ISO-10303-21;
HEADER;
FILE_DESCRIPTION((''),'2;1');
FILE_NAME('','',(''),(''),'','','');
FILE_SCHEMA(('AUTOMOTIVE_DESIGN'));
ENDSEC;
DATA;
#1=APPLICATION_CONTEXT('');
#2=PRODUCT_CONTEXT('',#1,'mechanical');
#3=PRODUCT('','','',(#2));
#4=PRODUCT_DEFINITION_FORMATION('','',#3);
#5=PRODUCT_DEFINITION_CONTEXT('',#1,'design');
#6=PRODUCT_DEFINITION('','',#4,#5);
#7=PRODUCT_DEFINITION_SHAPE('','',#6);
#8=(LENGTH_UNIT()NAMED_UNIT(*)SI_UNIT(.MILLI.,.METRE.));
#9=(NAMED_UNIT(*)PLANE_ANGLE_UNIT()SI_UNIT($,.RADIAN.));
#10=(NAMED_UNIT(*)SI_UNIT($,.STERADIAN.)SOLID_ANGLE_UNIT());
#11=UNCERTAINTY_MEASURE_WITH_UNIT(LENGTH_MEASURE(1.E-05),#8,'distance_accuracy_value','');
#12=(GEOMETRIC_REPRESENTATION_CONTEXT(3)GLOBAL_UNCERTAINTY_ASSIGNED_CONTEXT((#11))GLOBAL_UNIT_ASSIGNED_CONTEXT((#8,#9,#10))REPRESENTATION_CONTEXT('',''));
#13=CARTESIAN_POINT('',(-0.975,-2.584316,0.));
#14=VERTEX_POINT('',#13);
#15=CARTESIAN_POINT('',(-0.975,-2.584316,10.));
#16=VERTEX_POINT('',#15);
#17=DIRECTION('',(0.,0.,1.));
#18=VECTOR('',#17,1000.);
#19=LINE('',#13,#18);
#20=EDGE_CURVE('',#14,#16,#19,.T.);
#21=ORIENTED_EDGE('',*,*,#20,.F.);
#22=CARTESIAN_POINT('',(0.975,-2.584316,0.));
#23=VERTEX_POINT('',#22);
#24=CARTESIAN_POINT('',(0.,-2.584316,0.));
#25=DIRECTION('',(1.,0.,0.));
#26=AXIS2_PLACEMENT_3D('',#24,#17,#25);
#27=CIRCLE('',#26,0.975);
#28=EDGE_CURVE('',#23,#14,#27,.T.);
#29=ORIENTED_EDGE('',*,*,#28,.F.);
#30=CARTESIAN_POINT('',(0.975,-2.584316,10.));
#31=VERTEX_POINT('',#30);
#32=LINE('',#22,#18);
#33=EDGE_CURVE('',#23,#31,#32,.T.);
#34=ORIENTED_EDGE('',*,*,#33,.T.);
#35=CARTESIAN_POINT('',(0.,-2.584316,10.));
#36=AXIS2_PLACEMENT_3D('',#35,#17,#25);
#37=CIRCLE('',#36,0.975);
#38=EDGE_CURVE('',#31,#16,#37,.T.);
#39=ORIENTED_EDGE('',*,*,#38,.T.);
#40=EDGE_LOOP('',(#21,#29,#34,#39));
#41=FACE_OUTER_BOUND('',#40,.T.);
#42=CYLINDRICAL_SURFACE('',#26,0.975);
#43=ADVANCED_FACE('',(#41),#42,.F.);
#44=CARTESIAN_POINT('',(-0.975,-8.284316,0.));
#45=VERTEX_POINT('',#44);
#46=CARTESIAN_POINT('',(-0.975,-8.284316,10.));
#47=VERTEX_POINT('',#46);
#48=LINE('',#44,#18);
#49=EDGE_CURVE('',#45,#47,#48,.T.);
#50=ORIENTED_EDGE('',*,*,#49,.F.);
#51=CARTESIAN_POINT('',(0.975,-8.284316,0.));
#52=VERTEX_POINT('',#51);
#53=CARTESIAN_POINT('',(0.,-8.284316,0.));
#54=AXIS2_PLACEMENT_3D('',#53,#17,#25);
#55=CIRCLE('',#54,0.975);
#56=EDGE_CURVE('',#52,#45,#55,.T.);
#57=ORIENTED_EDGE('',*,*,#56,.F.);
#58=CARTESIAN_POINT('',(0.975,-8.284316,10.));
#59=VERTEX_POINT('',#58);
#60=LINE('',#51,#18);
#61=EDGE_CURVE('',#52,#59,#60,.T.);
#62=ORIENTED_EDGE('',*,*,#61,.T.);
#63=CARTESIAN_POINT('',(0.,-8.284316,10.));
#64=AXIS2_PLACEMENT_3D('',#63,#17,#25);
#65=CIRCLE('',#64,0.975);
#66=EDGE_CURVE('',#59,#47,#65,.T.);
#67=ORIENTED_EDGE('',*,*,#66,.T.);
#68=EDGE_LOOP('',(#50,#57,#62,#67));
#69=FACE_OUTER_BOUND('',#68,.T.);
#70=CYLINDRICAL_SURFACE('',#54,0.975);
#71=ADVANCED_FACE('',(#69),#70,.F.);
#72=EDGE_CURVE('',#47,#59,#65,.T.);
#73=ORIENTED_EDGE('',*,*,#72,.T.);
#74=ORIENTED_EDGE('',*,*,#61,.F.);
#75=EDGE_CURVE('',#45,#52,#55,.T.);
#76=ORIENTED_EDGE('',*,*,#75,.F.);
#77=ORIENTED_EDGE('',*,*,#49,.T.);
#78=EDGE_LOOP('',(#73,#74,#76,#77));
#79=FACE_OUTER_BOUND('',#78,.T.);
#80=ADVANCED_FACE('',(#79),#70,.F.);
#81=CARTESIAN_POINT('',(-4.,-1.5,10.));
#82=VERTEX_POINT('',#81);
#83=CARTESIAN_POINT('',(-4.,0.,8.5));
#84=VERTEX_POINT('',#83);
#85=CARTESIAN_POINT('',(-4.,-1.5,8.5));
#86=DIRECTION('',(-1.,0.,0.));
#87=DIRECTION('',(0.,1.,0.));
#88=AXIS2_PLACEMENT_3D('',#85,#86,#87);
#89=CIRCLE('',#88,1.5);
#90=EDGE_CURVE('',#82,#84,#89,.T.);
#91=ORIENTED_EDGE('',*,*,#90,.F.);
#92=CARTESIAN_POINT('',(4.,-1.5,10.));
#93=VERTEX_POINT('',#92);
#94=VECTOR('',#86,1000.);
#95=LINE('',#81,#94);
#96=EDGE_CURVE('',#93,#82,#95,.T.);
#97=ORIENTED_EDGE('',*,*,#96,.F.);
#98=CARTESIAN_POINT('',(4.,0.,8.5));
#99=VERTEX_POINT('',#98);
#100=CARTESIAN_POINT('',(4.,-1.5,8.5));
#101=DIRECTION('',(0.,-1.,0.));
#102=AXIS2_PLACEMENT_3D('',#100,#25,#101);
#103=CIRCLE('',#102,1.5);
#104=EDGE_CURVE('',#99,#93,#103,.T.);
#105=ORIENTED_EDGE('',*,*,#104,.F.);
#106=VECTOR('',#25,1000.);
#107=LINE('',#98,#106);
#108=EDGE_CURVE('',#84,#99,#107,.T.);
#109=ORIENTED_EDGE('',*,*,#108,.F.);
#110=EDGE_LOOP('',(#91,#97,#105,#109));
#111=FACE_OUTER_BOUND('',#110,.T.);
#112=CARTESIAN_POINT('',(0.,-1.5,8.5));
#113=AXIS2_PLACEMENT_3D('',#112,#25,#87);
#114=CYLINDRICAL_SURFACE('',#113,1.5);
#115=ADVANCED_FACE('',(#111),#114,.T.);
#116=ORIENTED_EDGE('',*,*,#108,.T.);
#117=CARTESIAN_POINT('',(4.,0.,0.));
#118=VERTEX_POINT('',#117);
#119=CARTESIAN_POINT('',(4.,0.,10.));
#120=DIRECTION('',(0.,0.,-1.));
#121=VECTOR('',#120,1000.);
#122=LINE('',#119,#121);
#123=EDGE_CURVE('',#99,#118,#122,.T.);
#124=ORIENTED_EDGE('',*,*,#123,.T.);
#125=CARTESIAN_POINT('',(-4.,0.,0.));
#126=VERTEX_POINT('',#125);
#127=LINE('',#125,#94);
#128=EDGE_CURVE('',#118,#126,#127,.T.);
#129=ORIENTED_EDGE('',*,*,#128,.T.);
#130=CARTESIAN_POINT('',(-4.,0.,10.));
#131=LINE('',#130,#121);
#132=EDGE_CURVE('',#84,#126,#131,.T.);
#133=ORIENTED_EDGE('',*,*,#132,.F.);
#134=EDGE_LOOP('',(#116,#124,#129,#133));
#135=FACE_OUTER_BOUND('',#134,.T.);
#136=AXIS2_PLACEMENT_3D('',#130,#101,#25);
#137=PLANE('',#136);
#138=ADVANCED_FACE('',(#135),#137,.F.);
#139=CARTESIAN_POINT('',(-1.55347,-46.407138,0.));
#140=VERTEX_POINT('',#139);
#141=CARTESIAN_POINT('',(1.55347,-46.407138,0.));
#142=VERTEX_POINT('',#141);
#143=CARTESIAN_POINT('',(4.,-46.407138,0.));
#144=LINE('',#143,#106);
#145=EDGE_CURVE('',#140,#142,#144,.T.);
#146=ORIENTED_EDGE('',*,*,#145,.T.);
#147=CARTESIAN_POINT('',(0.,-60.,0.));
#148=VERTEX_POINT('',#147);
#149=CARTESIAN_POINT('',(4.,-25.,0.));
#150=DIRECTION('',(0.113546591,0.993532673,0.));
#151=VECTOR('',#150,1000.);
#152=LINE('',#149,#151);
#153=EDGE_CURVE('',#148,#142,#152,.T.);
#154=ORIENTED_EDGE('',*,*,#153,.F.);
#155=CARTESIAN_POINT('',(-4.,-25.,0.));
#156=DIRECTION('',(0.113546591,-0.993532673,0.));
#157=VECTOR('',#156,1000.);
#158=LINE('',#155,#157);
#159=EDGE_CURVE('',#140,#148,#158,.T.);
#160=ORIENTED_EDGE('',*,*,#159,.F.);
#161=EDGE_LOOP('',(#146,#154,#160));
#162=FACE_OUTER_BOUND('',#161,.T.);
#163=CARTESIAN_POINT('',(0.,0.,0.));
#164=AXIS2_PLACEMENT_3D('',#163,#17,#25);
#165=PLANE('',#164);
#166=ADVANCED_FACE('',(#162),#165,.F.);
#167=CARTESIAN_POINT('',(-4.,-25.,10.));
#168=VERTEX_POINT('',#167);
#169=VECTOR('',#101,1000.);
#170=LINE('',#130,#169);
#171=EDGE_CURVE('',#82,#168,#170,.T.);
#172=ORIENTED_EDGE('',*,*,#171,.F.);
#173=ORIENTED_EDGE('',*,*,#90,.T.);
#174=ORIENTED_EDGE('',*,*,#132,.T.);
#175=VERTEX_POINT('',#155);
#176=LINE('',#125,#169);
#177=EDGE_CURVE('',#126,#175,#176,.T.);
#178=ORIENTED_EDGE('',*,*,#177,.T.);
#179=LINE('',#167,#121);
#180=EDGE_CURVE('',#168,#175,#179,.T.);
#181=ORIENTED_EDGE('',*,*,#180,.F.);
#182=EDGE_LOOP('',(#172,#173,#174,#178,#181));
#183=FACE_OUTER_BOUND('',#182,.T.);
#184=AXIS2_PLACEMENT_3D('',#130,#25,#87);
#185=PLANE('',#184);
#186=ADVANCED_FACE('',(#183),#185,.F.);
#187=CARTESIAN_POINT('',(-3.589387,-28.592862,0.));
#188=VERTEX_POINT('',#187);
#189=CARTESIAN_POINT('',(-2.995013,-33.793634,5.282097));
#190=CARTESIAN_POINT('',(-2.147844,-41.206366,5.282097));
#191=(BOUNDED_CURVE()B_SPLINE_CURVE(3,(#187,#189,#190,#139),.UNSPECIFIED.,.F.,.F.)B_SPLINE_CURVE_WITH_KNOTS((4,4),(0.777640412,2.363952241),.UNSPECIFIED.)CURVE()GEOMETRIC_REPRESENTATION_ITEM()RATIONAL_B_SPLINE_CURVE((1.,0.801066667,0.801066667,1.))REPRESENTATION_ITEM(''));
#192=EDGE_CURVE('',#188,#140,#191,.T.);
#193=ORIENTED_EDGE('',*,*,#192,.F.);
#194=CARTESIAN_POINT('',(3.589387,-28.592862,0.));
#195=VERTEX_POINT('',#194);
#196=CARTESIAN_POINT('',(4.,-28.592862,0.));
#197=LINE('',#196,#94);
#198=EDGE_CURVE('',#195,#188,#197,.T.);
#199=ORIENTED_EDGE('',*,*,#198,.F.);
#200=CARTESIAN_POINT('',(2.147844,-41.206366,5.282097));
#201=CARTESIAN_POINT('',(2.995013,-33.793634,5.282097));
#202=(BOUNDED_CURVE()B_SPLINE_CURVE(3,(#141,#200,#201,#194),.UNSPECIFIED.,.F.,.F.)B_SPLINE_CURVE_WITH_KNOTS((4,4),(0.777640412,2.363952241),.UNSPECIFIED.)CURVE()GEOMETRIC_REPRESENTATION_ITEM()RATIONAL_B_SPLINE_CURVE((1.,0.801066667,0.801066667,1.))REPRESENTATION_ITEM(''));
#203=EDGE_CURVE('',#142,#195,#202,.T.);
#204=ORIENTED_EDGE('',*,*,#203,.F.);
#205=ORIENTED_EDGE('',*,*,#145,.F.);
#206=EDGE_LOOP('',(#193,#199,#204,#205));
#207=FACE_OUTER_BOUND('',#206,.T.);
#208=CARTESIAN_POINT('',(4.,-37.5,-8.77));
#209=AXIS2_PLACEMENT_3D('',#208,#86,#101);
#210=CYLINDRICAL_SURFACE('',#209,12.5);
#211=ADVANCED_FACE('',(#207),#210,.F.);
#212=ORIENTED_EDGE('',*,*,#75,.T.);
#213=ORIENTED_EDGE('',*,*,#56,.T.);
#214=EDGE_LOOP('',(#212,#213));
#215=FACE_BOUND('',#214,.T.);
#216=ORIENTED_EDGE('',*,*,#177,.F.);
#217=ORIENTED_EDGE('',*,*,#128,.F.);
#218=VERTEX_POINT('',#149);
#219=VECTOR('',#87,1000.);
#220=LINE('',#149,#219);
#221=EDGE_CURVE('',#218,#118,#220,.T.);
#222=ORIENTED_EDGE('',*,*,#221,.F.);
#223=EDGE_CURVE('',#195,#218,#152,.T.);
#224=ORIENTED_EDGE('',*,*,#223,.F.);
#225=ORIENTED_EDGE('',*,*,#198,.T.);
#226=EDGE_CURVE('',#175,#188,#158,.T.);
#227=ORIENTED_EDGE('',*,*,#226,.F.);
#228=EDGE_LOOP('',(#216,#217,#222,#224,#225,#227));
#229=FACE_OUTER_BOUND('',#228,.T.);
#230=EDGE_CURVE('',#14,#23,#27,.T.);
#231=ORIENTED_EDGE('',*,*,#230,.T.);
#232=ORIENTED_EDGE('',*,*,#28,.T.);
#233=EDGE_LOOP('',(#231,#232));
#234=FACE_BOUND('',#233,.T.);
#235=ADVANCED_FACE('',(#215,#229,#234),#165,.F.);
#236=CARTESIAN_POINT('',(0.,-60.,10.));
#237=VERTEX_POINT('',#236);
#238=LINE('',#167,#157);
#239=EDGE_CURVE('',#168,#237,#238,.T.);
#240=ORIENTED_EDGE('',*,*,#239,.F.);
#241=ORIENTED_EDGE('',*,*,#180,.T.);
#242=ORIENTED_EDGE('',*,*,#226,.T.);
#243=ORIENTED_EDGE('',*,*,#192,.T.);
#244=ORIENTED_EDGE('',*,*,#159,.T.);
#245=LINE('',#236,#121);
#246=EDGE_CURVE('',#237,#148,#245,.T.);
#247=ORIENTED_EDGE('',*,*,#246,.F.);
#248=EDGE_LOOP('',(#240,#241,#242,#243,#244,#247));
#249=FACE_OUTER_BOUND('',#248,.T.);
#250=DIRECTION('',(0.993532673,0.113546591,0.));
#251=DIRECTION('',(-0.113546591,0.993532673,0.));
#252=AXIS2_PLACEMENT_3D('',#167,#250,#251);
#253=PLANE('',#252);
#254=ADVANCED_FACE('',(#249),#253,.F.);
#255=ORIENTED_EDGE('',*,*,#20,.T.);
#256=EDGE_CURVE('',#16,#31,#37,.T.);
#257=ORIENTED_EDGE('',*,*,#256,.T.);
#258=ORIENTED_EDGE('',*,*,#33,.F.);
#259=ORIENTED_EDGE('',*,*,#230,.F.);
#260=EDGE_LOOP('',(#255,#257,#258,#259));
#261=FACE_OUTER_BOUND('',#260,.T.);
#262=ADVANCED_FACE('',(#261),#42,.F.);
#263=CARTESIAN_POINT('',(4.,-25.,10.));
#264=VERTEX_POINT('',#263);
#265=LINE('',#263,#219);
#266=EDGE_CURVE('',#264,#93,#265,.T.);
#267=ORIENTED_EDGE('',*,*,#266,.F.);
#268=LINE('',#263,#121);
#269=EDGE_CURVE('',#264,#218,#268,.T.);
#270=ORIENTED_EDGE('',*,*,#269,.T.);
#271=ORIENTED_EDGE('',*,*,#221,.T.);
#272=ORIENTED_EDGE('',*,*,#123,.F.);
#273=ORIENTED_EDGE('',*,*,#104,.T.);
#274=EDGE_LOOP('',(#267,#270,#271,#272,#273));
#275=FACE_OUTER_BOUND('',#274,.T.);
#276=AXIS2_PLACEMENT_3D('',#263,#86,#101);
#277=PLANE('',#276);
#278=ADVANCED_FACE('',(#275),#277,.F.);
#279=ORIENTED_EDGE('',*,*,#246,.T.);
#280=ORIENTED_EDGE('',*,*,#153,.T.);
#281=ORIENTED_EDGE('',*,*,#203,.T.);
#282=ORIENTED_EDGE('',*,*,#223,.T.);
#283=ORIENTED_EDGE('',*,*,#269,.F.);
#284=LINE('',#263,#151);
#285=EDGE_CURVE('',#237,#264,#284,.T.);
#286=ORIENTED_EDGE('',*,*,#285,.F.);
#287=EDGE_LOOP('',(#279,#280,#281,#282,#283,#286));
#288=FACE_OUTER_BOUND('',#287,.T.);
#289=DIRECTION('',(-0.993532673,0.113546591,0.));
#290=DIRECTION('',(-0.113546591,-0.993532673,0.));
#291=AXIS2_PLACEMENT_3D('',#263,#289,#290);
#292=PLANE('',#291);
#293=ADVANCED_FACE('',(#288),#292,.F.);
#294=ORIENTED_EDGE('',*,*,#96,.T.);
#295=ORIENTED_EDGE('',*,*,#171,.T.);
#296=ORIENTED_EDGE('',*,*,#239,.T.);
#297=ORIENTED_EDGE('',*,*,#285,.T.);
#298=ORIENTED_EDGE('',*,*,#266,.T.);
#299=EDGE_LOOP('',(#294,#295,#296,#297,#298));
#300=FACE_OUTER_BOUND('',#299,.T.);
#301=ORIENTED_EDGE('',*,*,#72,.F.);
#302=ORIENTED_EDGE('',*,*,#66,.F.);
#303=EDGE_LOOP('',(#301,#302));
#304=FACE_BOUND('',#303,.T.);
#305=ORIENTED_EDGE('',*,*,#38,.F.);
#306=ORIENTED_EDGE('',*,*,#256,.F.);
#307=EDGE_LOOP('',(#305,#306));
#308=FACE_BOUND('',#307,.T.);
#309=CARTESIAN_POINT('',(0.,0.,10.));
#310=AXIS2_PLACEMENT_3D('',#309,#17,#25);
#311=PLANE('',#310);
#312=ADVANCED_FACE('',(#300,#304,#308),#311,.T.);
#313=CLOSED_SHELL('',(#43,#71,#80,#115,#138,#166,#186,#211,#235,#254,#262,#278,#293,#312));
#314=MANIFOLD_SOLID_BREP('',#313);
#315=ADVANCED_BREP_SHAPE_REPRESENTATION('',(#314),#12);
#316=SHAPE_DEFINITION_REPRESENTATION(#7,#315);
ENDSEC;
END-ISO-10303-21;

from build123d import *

# Parameters (mm, degrees)
EXTRUDE_1_DEPTH          = 10
SKETCH_3_R               = 0.975
CUT_EXTRUDE_2_DEPTH      = 61.959002617
FILLET_1_R               = 1.5
CUT_EXTRUDE_3_DEPTH      = 62.351446601
CUT_EXTRUDE_3_DEPTH_BACK = 62.351446601
SKETCH_6_R               = 12.5


with BuildPart() as part:
    # 草图1 → 凸台-拉伸1 (new body)
    with BuildSketch(Plane.XY):
        Polygon((-4, 0), (4, 0), (4, -25), (0, -60), (-4, -25), align=None)
    extrude(amount=EXTRUDE_1_DEPTH)

    # 草图3 → 切除-拉伸2 (cut, through all)
    with BuildSketch(Plane.XY.offset(10)):
        with Locations((0, -8.284315822)):
            Circle(SKETCH_3_R)
        with Locations((0, -2.584315822)):
            Circle(SKETCH_3_R)
    extrude(amount=-CUT_EXTRUDE_2_DEPTH, mode=Mode.SUBTRACT)

    # 圆角1
    fillet_1_edges = [part.edges().sort_by_distance(p)[0] for p in [
        (0, 0, 10),
    ]]
    fillet(fillet_1_edges, radius=FILLET_1_R)

    # 草图6 → 切除-拉伸3 (cut, two sides: drawn at the far end of the back side and taken through both)
    with BuildSketch(Plane.ZY.offset(4).offset(-CUT_EXTRUDE_3_DEPTH_BACK)):
        with Locations((-8.77, -37.5)):
            Circle(SKETCH_6_R)
    extrude(amount=CUT_EXTRUDE_3_DEPTH + CUT_EXTRUDE_3_DEPTH_BACK, mode=Mode.SUBTRACT)


solid = part.part
